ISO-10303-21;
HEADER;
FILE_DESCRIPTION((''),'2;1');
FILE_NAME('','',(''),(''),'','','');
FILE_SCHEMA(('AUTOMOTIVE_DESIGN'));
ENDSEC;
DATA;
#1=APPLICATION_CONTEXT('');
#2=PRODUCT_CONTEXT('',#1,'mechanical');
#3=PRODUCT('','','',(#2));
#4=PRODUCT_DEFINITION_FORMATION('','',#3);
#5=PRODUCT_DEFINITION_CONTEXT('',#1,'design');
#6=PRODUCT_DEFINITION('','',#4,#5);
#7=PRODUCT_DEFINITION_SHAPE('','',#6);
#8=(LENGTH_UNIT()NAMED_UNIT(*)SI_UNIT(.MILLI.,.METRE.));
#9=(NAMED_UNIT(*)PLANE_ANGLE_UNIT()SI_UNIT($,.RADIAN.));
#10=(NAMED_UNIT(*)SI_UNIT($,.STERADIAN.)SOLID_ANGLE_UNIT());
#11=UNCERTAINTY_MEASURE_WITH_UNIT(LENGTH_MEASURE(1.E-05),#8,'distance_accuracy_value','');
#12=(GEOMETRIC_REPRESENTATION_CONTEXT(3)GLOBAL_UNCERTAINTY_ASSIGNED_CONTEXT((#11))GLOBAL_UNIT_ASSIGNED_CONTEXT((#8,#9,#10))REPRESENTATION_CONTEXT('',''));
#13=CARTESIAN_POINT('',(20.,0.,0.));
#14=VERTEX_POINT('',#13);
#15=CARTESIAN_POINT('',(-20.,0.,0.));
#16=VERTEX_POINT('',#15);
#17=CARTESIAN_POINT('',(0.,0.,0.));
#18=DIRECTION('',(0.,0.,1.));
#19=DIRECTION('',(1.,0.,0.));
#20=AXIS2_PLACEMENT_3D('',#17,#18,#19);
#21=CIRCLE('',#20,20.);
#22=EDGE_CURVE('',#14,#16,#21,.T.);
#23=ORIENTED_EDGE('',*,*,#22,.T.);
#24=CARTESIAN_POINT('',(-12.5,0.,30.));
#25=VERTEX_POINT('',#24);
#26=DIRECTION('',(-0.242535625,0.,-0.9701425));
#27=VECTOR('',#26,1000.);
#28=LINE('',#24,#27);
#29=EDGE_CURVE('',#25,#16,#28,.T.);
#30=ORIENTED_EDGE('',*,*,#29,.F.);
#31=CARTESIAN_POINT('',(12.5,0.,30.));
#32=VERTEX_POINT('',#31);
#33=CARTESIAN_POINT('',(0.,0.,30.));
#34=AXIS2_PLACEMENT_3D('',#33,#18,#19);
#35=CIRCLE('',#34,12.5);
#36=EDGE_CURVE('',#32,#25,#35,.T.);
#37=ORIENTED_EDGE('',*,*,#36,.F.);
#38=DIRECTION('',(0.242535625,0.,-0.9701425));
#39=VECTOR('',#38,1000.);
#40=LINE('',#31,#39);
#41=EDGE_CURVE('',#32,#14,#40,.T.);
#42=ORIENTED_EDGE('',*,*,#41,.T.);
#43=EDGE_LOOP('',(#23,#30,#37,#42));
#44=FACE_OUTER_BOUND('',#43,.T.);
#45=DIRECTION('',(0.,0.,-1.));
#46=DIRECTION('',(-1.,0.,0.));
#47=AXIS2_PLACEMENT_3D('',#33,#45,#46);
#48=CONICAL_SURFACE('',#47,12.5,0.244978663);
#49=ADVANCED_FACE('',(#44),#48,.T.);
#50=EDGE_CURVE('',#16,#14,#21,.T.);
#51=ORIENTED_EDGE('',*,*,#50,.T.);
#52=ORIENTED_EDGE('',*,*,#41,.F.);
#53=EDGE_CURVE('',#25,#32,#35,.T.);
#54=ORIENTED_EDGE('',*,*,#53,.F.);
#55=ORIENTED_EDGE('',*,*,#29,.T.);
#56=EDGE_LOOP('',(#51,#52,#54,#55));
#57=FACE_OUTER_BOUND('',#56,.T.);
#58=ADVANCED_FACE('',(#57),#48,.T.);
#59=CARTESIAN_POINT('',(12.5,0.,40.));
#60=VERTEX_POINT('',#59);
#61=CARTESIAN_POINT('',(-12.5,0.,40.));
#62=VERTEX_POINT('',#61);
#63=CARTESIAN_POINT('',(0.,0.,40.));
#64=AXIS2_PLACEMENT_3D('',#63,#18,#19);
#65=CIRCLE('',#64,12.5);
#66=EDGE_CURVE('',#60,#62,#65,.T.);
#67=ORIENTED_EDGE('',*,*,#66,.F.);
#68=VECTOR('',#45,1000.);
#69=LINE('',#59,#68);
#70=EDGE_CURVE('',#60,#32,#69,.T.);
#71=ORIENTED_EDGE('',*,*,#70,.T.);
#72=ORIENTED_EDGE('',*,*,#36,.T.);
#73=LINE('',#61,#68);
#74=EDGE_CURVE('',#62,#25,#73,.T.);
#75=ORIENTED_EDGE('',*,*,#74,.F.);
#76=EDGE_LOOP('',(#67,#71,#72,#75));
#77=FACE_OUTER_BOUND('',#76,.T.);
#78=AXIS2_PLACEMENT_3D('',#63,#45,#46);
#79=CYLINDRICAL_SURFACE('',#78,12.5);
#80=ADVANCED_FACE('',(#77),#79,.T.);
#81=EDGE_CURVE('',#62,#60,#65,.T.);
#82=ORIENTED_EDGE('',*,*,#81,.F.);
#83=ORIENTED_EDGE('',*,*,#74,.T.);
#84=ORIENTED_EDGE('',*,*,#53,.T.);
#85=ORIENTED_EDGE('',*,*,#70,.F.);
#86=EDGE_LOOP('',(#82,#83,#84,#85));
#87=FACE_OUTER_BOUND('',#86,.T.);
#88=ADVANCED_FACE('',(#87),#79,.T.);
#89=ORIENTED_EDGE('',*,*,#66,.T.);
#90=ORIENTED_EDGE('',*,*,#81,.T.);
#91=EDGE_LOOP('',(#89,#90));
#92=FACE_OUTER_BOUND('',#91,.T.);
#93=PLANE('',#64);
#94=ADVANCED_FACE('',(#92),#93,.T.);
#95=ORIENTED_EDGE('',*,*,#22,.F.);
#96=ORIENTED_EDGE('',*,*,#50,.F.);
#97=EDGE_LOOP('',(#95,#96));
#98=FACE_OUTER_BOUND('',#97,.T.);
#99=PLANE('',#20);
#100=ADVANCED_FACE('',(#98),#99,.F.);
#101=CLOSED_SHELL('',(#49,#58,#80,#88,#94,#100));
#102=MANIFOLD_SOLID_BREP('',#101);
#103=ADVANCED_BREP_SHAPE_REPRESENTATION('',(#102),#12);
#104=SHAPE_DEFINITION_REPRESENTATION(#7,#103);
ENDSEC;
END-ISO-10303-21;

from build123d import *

# Parameters (mm, degrees)
SKETCH2_R           = 12.5
SKETCH1_R           = 20
SKETCH3_R           = 12.5
BOSS_EXTRUDE1_DEPTH = 10


with BuildPart() as part:
    # Sketch2 → Loft1 section 0
    with BuildSketch(Plane(origin=(0, 0, 30), x_dir=(-1, 0, 0), z_dir=(0, 0, -1))):
        Circle(SKETCH2_R)
    # Sketch1 → Loft1 section 1
    with BuildSketch(Plane.XY):
        Circle(SKETCH1_R)
    loft()

    # Sketch3 → Boss-Extrude1 (add)
    with BuildSketch(Plane.XY.offset(30)):
        Circle(SKETCH3_R)
    extrude(amount=BOSS_EXTRUDE1_DEPTH)


solid = part.part
